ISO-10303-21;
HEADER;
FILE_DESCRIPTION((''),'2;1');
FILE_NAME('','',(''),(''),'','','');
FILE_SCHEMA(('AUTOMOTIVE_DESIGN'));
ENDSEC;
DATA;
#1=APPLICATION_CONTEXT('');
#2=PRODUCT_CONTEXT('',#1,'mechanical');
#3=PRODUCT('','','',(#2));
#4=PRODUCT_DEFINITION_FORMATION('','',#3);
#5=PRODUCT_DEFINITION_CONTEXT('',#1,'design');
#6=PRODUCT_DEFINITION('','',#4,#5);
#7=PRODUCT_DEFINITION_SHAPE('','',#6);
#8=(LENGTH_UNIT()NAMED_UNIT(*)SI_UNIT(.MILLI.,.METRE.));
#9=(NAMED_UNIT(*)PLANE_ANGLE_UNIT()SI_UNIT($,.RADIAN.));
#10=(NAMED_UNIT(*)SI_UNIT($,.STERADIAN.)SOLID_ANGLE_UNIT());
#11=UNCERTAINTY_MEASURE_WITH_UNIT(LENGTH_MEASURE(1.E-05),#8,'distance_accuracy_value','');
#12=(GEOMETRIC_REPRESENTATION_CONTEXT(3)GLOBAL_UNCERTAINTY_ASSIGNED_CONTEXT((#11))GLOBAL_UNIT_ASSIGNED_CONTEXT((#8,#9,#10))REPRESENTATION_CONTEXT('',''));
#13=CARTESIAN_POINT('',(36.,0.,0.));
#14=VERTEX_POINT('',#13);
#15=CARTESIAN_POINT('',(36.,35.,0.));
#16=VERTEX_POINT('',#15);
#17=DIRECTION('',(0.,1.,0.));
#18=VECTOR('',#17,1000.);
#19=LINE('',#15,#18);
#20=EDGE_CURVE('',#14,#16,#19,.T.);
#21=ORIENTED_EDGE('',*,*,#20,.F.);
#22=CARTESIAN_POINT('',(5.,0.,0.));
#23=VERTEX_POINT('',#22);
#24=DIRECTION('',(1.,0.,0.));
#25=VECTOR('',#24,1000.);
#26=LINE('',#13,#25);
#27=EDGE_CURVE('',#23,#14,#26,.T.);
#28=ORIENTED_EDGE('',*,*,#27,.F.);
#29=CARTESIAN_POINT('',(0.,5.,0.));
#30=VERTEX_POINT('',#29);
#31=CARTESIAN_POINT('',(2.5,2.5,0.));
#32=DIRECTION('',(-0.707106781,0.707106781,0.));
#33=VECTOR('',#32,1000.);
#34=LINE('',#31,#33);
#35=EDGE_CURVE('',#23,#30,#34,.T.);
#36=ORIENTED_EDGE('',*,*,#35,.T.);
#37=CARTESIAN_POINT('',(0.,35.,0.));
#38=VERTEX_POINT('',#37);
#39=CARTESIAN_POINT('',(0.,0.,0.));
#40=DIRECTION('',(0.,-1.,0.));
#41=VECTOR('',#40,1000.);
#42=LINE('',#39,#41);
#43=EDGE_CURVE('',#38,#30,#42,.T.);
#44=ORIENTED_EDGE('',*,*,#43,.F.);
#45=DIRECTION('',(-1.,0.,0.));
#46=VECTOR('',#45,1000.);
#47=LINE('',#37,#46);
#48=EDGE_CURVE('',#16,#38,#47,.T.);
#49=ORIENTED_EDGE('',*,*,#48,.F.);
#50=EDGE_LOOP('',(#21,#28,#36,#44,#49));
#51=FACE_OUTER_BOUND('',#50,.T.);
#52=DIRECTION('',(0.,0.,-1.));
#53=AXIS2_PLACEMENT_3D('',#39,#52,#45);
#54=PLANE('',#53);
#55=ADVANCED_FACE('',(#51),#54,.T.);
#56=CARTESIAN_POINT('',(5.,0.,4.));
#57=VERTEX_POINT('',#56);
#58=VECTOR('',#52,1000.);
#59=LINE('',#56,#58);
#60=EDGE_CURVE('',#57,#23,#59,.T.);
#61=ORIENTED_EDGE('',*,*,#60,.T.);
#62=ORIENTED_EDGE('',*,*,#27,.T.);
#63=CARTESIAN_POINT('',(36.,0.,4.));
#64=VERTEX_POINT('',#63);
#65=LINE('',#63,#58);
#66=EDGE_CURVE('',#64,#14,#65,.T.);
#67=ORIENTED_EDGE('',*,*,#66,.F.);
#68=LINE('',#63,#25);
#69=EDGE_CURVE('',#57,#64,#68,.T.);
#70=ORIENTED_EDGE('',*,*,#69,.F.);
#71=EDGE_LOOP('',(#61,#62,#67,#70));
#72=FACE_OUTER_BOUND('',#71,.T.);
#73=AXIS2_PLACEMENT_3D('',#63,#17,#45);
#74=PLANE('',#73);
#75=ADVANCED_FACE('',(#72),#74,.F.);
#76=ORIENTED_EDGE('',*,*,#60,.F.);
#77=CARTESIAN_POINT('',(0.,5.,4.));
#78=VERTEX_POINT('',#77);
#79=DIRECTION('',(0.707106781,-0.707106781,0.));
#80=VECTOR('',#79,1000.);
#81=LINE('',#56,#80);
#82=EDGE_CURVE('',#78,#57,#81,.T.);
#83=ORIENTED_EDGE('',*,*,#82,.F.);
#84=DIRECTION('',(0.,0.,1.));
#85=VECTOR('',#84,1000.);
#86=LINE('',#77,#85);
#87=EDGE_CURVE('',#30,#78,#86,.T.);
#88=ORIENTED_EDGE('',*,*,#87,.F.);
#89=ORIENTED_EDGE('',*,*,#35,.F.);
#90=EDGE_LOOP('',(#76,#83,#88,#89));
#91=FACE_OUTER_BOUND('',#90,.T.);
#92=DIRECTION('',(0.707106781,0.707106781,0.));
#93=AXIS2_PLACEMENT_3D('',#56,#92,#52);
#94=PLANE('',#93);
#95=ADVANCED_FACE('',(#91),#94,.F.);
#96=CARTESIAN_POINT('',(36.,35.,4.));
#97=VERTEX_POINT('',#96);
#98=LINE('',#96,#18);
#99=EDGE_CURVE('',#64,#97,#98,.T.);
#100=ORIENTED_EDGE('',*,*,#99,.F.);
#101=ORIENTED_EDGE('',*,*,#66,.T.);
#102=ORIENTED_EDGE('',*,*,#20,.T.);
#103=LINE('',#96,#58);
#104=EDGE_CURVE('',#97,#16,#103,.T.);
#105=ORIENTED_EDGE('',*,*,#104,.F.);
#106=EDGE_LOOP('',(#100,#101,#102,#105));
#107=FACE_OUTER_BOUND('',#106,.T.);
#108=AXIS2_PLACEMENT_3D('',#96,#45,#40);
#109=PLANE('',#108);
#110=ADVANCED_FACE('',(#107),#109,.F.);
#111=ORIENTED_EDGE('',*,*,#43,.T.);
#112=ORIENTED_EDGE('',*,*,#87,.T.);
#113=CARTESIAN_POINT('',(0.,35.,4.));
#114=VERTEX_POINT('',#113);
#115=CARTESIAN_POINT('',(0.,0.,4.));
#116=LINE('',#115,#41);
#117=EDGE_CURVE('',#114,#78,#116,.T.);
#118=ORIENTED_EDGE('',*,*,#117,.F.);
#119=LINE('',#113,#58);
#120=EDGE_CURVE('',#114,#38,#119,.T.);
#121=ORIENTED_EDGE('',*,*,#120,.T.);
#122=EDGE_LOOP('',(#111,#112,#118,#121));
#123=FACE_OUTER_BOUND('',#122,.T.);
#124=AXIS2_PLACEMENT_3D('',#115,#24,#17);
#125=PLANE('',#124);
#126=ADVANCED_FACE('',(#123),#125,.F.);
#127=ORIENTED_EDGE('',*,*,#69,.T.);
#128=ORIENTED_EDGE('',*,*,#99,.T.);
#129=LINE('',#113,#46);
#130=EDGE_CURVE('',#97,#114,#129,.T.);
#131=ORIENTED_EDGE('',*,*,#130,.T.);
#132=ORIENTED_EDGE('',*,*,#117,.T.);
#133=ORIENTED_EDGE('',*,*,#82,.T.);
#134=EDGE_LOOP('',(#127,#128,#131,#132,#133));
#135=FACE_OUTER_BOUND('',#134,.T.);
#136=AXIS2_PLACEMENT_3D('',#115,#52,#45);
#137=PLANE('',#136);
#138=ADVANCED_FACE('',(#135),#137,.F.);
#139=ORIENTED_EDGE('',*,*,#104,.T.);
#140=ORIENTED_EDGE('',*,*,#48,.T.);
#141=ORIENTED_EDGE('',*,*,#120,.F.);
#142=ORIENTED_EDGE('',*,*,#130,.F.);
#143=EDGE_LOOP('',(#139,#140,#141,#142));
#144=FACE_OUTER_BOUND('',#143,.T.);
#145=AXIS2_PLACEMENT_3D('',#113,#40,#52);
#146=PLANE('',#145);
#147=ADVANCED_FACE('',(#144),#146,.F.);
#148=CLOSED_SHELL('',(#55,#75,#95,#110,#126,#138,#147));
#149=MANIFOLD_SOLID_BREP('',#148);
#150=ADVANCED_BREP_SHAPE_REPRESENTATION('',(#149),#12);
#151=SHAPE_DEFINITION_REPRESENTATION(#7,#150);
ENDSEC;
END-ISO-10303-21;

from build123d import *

# Parameters (mm, degrees)
SKETCH1_W           = 36
SKETCH1_H           = 35
BOSS_EXTRUDE1_DEPTH = 4
CHAMFER1_SIZE       = 5


with BuildPart() as part:
    # Sketch1 → Boss-Extrude1 (new body)
    with BuildSketch(Plane.XY):
        with Locations((18, 17.5)):
            Rectangle(SKETCH1_W, SKETCH1_H)
    extrude(amount=BOSS_EXTRUDE1_DEPTH)

    # Chamfer1
    chamfer1_edges = [part.edges().sort_by_distance(p)[0] for p in [
        (0, 0, 2),
    ]]
    chamfer(chamfer1_edges, length=CHAMFER1_SIZE)


solid = part.part
